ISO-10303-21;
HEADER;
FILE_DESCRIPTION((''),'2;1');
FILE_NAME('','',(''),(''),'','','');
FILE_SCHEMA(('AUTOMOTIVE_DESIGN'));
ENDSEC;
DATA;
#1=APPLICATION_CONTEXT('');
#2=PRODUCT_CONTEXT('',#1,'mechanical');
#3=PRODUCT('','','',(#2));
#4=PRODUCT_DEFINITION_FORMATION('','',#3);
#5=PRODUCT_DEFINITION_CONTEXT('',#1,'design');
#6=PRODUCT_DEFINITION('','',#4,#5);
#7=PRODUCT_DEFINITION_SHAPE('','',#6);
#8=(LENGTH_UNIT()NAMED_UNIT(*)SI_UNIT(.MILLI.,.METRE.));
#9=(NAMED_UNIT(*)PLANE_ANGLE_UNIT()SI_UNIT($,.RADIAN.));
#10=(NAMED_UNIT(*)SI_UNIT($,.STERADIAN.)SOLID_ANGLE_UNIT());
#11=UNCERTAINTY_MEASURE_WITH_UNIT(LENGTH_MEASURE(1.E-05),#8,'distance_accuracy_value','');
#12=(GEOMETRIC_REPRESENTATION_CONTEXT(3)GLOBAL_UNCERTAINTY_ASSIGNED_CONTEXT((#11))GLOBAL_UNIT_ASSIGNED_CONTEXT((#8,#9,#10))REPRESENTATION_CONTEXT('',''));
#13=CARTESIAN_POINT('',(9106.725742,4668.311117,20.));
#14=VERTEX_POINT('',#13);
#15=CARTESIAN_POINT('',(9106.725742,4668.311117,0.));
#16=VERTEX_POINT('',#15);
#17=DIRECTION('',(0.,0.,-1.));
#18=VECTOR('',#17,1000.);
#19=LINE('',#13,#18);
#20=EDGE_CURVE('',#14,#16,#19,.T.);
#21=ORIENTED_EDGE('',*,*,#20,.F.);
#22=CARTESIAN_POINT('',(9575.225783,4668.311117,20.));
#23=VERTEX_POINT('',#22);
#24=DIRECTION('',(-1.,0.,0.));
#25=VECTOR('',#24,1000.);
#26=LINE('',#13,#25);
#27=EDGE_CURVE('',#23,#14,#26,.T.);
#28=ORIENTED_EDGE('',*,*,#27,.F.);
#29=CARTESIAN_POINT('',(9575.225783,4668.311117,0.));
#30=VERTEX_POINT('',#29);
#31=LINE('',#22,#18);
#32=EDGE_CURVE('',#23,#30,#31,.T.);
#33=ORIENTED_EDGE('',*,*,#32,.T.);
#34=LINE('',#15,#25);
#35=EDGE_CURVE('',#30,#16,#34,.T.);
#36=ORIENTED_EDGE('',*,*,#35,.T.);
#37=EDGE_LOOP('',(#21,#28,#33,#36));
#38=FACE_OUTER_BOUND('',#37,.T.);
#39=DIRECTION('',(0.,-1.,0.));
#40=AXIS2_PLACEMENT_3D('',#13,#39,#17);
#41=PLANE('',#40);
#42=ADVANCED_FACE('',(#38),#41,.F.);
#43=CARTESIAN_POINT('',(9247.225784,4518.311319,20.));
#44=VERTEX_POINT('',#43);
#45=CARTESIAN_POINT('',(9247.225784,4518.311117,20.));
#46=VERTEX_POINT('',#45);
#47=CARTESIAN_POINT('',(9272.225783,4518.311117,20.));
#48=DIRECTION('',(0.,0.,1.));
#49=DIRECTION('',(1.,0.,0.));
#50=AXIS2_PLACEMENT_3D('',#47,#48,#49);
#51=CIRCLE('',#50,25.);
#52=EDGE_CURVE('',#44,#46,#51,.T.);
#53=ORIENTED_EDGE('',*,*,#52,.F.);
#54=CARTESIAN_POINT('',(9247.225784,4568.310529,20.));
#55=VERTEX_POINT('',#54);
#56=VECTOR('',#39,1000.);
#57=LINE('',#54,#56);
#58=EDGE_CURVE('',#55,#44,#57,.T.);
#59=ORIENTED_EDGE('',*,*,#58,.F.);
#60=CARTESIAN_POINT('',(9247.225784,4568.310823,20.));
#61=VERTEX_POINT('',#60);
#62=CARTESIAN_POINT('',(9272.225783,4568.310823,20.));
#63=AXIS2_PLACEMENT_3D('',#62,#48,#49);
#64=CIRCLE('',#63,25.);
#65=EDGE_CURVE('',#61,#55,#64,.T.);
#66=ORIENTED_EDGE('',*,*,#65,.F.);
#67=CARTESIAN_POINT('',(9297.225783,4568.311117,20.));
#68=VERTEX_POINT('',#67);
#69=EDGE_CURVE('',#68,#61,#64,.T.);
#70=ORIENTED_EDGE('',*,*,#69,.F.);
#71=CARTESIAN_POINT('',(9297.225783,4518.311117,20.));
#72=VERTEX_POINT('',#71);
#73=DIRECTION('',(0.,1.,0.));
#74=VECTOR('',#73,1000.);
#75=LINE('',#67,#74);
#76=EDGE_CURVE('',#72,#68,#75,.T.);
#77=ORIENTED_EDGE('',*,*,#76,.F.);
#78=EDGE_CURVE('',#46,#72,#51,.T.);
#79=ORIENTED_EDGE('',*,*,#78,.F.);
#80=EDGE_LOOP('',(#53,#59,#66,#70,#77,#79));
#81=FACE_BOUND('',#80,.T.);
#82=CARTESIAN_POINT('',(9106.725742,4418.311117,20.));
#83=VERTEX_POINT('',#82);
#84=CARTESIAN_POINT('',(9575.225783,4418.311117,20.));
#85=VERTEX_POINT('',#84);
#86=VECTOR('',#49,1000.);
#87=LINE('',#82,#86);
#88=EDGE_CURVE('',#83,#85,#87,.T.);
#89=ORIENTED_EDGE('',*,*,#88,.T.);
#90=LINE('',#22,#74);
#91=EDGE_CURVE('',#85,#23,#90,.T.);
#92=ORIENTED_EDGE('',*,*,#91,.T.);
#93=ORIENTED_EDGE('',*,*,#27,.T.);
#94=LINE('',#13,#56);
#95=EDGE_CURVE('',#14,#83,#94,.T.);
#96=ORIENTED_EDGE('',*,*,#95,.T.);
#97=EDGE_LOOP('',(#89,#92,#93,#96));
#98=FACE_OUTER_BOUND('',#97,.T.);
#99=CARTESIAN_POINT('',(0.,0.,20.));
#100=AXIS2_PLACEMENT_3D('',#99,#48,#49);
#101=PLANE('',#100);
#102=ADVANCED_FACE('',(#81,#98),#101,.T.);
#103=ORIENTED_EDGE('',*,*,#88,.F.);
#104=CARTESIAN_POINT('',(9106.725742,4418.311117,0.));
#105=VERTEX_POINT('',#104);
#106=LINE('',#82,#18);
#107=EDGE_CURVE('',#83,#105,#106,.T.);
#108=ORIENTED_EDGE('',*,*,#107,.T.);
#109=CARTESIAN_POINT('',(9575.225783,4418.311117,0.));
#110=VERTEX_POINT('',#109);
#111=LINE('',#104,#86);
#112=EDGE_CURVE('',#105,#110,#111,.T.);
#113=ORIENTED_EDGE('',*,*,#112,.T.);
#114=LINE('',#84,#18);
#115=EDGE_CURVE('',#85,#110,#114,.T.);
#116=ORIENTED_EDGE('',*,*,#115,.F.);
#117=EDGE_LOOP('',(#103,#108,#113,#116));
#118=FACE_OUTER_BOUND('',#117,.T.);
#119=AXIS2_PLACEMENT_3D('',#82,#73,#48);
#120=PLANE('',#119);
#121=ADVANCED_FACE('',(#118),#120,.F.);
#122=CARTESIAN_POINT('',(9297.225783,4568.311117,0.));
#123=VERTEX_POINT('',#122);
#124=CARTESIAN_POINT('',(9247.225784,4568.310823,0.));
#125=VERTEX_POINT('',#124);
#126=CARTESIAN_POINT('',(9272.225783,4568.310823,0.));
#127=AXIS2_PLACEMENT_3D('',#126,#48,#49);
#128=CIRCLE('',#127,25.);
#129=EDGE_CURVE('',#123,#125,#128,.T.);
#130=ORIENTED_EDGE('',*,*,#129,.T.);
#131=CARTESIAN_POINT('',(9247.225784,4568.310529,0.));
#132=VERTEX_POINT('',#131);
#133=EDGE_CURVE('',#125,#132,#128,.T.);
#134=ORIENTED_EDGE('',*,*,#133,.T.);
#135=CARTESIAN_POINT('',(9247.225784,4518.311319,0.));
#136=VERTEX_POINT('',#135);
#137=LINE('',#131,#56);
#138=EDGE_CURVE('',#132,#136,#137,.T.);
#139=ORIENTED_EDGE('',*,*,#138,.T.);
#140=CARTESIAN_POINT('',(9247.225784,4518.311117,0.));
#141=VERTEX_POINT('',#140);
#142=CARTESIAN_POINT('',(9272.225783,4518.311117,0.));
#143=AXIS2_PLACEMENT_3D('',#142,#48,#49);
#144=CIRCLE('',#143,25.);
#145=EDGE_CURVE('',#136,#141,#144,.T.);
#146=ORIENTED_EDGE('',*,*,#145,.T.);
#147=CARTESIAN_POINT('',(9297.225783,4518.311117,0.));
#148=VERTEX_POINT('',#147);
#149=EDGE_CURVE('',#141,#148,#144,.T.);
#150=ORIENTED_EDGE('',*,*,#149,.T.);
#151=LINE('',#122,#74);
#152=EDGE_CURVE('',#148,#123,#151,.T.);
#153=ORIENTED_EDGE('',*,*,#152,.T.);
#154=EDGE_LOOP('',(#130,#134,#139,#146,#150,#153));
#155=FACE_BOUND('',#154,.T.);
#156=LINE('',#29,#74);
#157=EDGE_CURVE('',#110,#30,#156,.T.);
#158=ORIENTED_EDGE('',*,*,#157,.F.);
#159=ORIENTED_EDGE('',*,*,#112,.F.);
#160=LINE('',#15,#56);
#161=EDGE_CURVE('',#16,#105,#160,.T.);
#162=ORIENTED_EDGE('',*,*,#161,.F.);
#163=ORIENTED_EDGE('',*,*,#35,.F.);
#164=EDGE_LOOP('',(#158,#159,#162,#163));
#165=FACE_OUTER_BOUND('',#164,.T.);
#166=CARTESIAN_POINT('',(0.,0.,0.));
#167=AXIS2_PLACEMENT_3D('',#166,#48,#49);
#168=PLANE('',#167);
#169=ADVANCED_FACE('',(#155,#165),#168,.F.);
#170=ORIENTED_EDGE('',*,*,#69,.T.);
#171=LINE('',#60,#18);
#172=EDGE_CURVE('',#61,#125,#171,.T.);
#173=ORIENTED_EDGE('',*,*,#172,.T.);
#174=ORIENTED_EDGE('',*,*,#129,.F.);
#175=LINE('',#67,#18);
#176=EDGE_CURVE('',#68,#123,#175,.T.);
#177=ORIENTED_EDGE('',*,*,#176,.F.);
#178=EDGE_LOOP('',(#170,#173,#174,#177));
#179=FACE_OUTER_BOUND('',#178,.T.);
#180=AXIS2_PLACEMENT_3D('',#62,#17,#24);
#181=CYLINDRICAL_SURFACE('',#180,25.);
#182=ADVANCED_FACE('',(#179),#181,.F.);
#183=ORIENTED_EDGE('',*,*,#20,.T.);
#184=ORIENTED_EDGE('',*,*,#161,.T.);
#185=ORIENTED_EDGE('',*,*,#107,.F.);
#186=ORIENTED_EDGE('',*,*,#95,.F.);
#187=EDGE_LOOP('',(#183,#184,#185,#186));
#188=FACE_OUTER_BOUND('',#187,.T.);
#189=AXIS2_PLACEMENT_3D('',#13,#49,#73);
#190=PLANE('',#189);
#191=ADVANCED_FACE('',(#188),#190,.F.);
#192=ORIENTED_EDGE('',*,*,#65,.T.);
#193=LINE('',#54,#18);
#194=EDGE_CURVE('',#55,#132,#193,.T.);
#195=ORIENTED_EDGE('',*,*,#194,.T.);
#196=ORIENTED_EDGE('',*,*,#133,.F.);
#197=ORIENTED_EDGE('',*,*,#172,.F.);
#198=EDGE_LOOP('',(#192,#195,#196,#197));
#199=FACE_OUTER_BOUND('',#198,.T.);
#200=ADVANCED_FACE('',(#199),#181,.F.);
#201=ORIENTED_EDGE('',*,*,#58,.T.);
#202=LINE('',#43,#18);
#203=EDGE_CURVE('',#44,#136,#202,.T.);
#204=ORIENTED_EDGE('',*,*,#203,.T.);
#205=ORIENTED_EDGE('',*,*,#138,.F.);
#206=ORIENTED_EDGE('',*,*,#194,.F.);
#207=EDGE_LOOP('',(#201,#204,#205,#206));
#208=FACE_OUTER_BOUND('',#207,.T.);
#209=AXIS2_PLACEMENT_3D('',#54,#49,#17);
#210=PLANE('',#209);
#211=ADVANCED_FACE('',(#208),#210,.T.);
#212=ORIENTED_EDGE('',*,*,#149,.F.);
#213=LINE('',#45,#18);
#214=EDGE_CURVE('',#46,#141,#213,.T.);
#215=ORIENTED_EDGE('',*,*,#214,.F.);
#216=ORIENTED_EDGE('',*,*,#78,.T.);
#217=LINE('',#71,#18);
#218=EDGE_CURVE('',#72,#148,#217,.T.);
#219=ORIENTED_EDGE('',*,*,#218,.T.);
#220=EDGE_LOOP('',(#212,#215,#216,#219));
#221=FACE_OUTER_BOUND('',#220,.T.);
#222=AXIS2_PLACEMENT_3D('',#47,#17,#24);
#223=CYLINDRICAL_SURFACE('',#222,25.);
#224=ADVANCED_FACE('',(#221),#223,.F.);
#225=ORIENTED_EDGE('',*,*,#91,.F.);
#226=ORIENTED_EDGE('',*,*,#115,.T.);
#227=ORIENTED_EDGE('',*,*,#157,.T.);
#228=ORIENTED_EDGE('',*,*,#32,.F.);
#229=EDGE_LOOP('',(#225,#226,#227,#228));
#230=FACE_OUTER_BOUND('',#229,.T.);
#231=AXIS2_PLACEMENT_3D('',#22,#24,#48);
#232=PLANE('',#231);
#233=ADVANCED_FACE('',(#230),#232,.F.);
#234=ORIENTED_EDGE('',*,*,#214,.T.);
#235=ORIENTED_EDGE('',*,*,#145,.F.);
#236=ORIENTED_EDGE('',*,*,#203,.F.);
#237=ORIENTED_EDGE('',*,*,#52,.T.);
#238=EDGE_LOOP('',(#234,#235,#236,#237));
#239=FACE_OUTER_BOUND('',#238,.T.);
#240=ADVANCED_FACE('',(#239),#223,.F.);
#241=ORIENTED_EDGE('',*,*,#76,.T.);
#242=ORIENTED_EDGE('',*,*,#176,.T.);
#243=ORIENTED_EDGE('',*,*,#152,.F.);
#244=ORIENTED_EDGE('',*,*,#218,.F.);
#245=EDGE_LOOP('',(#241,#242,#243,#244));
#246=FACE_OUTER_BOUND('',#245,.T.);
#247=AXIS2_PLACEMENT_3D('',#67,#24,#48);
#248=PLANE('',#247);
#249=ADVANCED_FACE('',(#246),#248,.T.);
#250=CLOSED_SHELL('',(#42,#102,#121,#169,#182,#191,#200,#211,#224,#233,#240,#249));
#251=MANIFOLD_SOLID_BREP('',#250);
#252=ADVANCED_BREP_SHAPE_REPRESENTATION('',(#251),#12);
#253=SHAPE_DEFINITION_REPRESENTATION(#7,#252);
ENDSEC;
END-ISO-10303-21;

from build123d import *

# Parameters (mm, degrees)
BOSS_EXTRUDE1_DEPTH = 20


with BuildPart() as part:
    # Sketch1 → Boss-Extrude1 (new body)
    with BuildSketch(Plane.XY):
        Polygon((9106.725741881, 4668.311117452), (9575.225782872, 4668.311117452), (9575.225782872, 4418.311117452), (9106.725741967, 4418.311117452), align=None)
        with BuildLine():
            Line((9247.225783525, 4568.310529412), (9247.225783525, 4518.311318924))
            ThreePointArc((9247.225783525, 4518.311318924), (9272.225682554, 4493.311117122), (9297.225783432, 4518.311117075))
            Line((9297.225783432, 4518.311117075), (9297.225783432, 4568.311116981))
            ThreePointArc((9297.225783432, 4568.311116981), (9272.225489694, 4593.31082315), (9247.225783525, 4568.310529412))
        make_face(mode=Mode.SUBTRACT)
    extrude(amount=BOSS_EXTRUDE1_DEPTH)


solid = part.part
